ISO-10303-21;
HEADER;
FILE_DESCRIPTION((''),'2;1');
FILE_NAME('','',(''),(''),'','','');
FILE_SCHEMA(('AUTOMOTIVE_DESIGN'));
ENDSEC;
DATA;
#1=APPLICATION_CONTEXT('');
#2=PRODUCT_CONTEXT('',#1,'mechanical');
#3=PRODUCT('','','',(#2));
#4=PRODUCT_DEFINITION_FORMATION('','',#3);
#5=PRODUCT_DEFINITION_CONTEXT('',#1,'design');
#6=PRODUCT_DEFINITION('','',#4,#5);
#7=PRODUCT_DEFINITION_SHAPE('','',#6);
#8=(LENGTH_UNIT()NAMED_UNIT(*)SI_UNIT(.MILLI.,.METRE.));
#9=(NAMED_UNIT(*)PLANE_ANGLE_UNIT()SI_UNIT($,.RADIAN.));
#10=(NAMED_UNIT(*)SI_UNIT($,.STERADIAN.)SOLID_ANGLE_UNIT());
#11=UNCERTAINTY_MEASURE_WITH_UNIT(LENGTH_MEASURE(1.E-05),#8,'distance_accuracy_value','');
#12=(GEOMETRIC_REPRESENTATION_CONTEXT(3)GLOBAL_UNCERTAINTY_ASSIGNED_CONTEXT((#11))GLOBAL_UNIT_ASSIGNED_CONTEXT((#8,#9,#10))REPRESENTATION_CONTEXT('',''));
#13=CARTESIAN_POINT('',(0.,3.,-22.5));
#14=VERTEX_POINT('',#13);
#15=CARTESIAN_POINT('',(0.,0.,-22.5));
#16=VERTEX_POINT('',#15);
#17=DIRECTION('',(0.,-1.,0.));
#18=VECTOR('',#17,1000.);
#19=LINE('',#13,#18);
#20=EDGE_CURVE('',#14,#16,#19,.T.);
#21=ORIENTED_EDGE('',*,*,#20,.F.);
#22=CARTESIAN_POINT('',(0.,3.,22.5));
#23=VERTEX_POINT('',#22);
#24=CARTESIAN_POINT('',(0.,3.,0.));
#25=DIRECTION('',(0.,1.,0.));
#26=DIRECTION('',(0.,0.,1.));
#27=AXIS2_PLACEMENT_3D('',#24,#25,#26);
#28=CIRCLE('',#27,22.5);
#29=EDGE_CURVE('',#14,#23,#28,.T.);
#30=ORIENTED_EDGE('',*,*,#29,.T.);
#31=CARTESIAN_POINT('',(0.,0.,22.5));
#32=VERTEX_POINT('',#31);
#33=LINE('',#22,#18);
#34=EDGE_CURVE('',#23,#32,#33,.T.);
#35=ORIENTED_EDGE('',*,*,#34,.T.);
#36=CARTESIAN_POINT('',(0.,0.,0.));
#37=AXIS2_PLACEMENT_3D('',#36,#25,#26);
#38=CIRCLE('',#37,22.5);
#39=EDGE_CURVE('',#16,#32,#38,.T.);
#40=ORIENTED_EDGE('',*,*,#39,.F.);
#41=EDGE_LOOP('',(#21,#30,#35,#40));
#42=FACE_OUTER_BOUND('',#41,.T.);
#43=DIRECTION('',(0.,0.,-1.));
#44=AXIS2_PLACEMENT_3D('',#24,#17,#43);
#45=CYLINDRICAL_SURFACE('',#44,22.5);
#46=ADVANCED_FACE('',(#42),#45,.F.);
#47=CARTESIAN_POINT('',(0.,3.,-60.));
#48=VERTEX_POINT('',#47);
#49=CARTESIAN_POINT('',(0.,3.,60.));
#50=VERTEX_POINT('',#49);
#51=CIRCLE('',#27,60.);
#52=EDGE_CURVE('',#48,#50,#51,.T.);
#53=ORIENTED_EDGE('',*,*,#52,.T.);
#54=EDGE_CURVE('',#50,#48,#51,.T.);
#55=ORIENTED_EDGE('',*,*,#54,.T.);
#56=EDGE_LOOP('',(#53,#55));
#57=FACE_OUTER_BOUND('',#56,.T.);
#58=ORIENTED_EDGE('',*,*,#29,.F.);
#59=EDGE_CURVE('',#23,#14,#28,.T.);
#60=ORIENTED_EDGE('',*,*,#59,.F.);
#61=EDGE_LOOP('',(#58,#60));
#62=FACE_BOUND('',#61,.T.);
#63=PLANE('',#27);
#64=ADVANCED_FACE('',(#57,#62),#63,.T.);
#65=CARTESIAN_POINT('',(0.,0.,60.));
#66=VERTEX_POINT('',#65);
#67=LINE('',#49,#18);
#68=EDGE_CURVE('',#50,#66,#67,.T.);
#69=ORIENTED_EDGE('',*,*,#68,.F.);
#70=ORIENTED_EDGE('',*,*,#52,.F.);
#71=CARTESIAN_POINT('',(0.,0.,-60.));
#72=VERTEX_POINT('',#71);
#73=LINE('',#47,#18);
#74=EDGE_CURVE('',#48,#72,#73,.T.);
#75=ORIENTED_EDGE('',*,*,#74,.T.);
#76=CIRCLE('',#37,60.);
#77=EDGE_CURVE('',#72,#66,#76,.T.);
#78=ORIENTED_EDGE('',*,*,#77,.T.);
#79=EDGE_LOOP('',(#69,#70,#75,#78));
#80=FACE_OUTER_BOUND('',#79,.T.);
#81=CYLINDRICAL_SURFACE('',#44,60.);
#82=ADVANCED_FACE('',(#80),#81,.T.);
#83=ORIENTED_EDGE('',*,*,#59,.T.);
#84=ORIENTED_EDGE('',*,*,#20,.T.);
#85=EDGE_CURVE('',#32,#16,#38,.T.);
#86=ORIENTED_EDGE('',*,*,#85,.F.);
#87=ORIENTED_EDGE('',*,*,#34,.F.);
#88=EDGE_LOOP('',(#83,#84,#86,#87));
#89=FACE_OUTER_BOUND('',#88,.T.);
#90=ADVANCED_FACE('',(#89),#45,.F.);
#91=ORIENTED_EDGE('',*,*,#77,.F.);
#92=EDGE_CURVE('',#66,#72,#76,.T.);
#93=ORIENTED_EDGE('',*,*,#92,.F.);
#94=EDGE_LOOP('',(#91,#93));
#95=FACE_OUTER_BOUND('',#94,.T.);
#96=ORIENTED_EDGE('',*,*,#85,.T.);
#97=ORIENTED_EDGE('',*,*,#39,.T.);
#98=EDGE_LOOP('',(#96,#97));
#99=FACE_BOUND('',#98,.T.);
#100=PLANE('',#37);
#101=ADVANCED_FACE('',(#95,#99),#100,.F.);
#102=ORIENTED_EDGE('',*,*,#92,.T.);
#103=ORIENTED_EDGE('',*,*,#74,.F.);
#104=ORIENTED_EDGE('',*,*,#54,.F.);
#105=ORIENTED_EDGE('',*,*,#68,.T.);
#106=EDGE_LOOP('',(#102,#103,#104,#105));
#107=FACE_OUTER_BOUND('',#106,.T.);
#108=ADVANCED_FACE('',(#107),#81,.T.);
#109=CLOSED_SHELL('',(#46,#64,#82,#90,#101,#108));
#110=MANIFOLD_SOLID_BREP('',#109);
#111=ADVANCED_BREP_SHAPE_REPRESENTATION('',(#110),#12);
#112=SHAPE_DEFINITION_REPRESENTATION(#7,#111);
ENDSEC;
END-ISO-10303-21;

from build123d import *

# Parameters (mm, degrees)
SKETCH1_R           = 60
SKETCH1_R_2         = 22.5
BOSS_EXTRUDE1_DEPTH = 3


with BuildPart() as part:
    # Sketch1 → Boss-Extrude1 (new body)
    with BuildSketch(Plane(origin=(0, 0, 0), x_dir=(1, 0, 0), z_dir=(0, 1, 0))):
        with Locations(Location((0, 0, 0), (0, 0, 270))):
            Circle(SKETCH1_R)
        with Locations(Location((0, 0, 0), (0, 0, 270))):
            Circle(SKETCH1_R_2, mode=Mode.SUBTRACT)
    extrude(amount=BOSS_EXTRUDE1_DEPTH)


solid = part.part
